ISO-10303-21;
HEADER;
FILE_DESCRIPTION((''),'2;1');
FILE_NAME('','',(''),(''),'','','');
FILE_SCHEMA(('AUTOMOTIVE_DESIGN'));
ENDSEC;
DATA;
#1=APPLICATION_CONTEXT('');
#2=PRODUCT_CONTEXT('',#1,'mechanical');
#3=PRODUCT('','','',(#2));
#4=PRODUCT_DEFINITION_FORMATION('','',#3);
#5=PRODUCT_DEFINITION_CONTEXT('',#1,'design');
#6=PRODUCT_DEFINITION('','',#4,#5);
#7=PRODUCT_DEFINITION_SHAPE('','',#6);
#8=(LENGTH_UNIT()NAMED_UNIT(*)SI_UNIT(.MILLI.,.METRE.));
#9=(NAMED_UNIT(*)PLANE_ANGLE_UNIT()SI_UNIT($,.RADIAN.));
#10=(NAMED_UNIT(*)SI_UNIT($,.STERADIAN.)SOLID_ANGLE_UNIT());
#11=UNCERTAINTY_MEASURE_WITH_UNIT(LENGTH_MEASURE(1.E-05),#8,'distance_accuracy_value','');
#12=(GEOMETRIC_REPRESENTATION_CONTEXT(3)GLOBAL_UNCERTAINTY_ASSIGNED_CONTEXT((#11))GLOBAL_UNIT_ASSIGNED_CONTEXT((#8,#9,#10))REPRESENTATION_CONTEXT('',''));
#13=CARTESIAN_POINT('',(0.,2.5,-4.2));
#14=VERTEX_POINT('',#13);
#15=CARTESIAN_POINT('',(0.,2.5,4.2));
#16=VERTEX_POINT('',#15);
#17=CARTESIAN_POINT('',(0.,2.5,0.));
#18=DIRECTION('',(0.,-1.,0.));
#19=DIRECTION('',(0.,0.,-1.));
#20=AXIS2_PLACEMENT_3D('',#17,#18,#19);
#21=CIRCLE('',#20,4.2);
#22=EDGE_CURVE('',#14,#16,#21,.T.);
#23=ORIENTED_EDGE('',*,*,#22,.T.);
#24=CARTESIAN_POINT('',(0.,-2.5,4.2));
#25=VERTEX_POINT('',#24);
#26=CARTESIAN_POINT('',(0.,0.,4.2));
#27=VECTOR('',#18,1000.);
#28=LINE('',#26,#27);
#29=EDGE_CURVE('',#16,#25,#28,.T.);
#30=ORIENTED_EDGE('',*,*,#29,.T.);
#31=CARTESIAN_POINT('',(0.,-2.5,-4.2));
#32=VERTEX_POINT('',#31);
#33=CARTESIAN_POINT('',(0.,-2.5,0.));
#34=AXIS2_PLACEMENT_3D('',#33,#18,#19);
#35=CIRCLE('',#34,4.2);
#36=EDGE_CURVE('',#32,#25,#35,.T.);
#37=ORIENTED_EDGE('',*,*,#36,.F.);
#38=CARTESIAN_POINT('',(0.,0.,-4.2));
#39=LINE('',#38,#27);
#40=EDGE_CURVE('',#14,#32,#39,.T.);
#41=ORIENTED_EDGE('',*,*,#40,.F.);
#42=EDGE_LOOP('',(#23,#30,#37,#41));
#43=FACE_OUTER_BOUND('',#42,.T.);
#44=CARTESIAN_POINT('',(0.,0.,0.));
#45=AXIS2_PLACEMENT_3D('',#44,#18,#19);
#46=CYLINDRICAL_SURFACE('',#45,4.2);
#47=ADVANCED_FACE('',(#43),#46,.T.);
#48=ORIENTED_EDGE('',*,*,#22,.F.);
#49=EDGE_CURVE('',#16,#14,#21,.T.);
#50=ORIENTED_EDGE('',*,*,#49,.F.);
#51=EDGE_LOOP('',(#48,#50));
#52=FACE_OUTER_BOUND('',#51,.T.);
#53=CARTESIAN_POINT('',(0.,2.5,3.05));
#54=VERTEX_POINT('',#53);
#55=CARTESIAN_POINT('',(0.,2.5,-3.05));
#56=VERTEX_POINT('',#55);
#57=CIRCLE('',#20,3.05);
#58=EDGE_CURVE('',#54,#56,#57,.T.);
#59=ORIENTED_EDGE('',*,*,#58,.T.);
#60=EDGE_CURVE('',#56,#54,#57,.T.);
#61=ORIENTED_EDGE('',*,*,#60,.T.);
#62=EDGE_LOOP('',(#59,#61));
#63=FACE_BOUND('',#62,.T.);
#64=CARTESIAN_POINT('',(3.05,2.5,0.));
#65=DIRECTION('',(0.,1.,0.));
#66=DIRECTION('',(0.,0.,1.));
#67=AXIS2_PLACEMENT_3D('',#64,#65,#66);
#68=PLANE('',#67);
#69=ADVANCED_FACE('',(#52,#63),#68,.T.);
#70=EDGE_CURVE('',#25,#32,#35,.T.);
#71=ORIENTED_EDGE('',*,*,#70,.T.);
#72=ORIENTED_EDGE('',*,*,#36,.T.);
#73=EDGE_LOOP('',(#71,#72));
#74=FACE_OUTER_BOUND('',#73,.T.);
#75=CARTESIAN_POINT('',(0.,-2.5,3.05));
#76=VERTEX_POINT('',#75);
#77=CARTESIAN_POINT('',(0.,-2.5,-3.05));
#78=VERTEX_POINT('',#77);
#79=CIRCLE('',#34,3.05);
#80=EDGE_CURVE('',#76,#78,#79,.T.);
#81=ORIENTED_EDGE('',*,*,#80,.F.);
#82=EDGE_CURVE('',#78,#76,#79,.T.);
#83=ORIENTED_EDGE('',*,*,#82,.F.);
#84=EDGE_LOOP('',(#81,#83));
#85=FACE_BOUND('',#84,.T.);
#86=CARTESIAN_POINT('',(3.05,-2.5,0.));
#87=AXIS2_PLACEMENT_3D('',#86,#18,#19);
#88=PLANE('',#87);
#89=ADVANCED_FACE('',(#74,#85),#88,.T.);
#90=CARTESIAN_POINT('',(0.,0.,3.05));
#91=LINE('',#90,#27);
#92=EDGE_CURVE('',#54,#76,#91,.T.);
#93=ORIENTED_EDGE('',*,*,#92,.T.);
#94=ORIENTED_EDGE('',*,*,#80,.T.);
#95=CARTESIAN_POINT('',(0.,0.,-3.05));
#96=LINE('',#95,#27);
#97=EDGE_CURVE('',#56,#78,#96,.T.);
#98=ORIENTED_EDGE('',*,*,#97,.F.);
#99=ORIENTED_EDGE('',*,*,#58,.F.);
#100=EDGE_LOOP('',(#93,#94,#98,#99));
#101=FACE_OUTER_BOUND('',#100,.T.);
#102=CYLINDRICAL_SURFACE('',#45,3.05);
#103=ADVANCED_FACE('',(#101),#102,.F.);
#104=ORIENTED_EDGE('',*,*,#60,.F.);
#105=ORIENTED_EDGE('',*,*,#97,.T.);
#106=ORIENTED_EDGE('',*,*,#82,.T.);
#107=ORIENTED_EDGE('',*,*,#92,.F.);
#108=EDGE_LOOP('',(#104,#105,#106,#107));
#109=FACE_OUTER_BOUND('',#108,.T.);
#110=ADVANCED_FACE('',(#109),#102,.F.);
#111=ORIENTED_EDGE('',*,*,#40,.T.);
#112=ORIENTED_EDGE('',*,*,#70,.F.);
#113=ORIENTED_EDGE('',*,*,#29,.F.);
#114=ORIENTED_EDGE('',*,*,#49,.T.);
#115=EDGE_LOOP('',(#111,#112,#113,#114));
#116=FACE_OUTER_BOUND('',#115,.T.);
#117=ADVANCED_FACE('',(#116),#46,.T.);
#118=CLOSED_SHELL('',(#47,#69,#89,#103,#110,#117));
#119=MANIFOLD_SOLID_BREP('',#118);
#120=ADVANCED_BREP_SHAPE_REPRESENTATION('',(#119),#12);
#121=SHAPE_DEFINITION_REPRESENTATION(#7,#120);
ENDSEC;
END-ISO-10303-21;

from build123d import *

# Parameters (mm, degrees)
SKETCH1_W = 1.15
SKETCH1_H = 5


with BuildPart() as part:
    # Sketch1 → Revolve1 (revolve)
    with BuildSketch(Plane.XY, mode=Mode.PRIVATE) as revolve1_sk:
        with Locations((3.625, 0)):
            Rectangle(SKETCH1_W, SKETCH1_H)
    revolve(revolve1_sk.sketch.rotate(Axis((0, 0, 0), (0, 1, 0)), 90), axis=Axis((0, 0, 0), (0, 1, 0)))


solid = part.part
